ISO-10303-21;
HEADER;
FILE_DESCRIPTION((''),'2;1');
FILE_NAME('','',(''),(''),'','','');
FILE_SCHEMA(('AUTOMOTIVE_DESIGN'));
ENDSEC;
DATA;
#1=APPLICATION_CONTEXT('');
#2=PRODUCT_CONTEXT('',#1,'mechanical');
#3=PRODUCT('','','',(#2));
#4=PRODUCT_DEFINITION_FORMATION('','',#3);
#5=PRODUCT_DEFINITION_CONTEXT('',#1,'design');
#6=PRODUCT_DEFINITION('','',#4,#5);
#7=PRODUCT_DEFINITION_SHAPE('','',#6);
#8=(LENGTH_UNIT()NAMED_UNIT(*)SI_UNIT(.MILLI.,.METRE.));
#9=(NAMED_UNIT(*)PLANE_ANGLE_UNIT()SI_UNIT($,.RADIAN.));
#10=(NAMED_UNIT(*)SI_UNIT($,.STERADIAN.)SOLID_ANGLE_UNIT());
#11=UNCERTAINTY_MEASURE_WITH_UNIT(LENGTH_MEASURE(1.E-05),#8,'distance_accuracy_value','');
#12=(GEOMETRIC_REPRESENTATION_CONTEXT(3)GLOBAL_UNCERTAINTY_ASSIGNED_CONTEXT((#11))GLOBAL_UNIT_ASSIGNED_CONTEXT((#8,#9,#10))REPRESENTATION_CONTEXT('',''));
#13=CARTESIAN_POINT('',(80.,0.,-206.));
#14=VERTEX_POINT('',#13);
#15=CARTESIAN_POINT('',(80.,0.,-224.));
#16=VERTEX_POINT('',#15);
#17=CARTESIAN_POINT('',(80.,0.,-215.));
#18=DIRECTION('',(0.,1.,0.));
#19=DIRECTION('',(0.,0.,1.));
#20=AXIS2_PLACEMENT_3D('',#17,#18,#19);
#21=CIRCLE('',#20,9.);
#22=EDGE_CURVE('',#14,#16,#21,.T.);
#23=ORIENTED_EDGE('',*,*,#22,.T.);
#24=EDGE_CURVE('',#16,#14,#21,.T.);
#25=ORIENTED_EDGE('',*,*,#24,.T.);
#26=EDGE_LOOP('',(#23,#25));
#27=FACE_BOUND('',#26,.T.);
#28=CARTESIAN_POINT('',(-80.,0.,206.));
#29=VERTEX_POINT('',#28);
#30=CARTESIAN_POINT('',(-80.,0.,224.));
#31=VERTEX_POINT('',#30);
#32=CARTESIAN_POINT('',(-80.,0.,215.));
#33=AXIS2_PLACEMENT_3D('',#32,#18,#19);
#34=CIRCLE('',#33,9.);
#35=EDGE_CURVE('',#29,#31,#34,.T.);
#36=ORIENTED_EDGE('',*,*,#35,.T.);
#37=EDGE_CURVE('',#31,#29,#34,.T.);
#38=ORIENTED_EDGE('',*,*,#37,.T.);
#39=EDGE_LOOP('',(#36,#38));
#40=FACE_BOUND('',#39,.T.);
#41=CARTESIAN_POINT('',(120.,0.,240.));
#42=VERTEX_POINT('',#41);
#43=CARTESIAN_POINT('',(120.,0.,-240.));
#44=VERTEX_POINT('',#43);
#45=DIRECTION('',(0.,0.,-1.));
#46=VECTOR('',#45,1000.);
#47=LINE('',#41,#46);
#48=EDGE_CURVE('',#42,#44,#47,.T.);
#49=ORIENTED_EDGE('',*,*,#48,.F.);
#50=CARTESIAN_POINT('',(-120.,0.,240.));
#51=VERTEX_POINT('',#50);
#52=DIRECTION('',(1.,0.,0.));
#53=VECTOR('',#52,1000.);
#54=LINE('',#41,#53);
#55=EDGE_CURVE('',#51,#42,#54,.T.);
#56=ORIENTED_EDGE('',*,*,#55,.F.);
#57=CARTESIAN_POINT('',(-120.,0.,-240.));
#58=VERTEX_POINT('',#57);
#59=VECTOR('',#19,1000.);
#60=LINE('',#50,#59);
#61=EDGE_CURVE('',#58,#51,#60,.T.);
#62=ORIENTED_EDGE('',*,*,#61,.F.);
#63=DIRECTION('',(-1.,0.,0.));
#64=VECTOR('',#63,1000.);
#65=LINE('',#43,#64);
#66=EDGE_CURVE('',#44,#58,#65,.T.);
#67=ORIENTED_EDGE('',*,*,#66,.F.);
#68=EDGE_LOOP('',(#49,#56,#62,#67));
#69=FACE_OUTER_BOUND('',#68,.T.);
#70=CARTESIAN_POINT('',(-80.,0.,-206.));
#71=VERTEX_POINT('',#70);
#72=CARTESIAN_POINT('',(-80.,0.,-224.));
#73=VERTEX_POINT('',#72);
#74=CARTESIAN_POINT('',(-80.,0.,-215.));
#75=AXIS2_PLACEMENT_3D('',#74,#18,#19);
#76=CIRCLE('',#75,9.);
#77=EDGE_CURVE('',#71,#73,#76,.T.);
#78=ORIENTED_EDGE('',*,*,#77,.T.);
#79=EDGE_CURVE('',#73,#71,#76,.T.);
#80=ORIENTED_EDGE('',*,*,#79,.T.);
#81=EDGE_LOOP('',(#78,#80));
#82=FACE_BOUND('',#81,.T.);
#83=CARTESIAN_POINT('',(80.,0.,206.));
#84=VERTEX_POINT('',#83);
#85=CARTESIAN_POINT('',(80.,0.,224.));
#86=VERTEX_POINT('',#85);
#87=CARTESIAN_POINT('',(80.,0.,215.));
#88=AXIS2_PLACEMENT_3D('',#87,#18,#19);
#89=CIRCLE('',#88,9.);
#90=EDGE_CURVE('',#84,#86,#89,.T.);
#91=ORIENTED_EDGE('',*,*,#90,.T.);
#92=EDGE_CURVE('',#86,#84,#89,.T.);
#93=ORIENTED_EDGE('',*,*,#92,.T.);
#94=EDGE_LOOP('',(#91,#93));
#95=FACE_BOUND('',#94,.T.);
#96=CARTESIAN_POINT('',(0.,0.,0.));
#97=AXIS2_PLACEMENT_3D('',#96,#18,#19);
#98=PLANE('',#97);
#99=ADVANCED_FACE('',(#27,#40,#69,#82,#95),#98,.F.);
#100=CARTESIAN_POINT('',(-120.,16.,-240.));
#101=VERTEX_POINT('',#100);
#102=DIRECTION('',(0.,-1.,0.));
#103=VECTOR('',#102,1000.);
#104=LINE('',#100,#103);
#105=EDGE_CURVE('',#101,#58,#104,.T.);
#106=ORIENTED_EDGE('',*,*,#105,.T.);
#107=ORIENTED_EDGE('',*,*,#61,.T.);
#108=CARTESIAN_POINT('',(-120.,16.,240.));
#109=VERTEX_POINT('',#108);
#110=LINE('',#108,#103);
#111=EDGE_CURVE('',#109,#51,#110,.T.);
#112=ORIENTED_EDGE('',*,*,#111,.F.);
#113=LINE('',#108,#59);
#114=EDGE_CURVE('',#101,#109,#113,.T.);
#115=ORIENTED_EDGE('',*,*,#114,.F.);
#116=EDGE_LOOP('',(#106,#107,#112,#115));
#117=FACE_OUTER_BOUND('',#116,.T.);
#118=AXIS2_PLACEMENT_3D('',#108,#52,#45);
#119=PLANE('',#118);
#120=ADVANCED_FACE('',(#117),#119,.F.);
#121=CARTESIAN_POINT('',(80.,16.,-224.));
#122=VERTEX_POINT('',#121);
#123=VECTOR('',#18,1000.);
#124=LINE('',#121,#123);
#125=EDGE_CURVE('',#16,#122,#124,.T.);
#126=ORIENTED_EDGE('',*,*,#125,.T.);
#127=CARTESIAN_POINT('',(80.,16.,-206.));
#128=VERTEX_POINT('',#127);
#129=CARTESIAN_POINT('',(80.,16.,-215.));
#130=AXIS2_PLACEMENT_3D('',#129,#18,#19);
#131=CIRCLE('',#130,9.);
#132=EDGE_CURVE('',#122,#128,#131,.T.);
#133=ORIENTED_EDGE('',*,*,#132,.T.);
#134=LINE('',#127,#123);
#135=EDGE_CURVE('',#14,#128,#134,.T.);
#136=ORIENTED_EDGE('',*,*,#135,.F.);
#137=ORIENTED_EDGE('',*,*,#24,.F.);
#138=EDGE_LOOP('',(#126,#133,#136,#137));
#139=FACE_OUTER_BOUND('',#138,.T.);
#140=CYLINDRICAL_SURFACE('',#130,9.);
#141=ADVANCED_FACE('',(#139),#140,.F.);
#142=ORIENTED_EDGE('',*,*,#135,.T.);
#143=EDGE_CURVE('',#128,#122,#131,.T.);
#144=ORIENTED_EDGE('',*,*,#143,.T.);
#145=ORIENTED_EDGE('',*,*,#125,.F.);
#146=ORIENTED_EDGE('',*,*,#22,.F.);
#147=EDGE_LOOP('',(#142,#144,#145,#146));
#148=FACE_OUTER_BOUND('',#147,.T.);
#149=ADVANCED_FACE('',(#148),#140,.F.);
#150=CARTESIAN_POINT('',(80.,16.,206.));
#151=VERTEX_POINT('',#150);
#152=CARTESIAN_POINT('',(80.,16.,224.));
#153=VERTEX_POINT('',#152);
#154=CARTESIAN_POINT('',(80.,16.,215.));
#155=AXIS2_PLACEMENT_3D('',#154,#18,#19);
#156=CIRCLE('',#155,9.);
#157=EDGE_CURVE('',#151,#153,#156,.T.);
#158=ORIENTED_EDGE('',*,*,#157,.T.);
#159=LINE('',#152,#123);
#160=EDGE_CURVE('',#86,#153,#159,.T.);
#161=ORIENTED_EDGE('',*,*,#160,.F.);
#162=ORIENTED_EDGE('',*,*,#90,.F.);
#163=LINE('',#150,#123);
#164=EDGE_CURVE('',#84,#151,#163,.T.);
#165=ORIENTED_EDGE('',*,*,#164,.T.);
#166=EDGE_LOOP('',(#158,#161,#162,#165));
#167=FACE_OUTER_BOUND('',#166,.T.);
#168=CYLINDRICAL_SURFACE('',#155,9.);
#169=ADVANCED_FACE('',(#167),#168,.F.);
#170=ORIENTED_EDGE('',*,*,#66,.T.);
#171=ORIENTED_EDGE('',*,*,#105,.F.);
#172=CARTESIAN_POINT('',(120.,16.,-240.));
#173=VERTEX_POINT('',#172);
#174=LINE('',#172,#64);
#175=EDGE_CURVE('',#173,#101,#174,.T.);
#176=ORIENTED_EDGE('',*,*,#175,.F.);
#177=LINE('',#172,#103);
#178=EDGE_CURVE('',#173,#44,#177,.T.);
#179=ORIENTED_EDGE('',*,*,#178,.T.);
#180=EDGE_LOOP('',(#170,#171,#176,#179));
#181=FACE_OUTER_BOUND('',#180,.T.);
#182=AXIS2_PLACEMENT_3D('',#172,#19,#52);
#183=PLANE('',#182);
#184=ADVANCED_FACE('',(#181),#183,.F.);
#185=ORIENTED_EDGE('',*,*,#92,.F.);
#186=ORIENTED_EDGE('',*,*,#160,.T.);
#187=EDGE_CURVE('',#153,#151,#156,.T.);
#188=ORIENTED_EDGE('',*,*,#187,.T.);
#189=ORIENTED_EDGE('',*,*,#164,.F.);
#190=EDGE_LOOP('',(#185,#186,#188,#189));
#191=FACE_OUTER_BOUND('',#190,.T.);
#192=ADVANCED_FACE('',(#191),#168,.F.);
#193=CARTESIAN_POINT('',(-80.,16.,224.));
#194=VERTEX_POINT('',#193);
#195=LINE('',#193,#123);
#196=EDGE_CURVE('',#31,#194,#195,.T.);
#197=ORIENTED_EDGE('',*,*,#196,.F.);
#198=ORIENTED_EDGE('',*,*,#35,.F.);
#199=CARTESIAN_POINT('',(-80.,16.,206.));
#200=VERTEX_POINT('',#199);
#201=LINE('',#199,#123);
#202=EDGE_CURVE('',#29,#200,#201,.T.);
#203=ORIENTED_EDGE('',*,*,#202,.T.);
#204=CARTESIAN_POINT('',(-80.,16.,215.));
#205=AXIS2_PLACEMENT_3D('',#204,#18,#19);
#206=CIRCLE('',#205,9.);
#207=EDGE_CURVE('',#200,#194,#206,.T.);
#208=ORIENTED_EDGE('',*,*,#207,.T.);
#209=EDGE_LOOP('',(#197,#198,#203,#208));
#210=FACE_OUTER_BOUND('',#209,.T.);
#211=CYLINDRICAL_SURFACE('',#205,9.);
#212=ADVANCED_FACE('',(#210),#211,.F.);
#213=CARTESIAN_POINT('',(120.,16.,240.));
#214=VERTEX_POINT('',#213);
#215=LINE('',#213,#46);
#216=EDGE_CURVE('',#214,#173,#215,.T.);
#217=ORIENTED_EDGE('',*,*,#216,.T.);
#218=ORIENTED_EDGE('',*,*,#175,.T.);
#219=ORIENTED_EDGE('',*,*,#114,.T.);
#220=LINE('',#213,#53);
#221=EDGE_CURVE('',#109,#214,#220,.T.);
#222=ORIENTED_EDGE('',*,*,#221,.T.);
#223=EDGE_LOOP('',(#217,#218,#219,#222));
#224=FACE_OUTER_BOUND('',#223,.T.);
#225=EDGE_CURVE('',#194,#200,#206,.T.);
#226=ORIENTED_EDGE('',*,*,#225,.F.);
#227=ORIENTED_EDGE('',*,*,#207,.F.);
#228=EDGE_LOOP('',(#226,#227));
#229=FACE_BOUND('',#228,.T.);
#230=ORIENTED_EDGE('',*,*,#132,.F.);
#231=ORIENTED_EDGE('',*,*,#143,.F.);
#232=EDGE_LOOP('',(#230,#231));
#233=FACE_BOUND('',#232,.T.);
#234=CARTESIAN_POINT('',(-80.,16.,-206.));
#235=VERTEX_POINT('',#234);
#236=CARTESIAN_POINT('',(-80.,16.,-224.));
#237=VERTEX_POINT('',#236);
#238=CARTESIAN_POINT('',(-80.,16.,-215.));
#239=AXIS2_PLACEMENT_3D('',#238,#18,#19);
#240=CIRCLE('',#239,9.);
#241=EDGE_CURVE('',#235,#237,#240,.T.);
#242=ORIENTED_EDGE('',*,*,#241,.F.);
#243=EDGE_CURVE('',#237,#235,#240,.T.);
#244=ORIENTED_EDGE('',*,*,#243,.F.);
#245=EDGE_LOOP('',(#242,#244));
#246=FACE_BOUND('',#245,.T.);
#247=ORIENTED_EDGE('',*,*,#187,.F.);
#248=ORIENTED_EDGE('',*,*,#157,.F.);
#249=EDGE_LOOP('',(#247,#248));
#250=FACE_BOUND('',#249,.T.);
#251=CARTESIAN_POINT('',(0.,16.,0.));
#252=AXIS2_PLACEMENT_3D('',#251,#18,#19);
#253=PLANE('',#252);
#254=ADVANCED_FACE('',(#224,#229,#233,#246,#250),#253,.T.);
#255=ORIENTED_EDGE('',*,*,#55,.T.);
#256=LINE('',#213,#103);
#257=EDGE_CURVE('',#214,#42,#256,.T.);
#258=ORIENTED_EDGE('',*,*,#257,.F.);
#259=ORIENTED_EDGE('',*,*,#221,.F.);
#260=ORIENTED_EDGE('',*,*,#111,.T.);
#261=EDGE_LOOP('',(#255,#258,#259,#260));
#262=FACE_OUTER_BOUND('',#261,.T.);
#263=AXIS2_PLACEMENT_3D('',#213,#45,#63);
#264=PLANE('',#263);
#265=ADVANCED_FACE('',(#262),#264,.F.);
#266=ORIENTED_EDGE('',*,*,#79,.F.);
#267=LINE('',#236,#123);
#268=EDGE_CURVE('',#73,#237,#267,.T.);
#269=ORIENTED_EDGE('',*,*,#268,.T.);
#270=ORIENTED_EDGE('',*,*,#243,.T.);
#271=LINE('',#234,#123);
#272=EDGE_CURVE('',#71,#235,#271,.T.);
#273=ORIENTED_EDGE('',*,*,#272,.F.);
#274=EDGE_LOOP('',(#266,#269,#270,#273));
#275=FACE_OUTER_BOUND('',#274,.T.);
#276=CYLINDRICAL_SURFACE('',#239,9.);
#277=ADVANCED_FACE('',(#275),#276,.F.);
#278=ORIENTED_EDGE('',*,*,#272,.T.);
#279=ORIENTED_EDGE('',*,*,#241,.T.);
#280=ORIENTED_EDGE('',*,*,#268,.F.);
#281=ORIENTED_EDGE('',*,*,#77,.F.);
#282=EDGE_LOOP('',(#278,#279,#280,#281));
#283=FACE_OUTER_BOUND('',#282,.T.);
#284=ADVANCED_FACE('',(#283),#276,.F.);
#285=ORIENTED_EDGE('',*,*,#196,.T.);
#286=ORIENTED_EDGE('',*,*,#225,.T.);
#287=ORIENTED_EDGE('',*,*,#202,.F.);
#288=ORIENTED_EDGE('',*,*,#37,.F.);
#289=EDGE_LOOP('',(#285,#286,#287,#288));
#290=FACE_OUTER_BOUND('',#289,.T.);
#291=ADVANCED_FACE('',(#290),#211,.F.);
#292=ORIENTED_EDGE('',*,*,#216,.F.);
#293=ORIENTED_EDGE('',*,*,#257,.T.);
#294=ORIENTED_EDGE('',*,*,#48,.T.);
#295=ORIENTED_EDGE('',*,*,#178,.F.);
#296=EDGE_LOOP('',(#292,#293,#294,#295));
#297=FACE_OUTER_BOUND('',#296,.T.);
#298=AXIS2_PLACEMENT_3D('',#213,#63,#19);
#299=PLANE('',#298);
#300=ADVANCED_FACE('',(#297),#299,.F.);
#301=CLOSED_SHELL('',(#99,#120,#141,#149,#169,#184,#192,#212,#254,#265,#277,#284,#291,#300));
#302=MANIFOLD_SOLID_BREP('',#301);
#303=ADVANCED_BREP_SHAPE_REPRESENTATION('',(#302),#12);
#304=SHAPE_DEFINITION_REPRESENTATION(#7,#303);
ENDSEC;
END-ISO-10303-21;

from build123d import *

# Parameters (mm, degrees)
SKETCH1_W                  = 240
SKETCH1_H                  = 480
BOSS_EXTRUDE1_DEPTH        = 16
F_18_0_18_DIAMETER_HOLE1_D = 18


with BuildPart() as part:
    # Sketch1 → Boss-Extrude1 (new body)
    with BuildSketch(Plane(origin=(0, 0, 0), x_dir=(1, 0, 0), z_dir=(0, 1, 0))):
        Rectangle(SKETCH1_W, SKETCH1_H)
    extrude(amount=BOSS_EXTRUDE1_DEPTH)

    # Ø18.0 (18) Diameter Hole1 (through all)
    with Locations(Plane(origin=(0, 16, 0), x_dir=(1, 0, 0), z_dir=(0, 1, 0))):
        with Locations((-80, -215), (80, -215), (80, 215), (-80, 215)):
            Hole(F_18_0_18_DIAMETER_HOLE1_D / 2)


solid = part.part
